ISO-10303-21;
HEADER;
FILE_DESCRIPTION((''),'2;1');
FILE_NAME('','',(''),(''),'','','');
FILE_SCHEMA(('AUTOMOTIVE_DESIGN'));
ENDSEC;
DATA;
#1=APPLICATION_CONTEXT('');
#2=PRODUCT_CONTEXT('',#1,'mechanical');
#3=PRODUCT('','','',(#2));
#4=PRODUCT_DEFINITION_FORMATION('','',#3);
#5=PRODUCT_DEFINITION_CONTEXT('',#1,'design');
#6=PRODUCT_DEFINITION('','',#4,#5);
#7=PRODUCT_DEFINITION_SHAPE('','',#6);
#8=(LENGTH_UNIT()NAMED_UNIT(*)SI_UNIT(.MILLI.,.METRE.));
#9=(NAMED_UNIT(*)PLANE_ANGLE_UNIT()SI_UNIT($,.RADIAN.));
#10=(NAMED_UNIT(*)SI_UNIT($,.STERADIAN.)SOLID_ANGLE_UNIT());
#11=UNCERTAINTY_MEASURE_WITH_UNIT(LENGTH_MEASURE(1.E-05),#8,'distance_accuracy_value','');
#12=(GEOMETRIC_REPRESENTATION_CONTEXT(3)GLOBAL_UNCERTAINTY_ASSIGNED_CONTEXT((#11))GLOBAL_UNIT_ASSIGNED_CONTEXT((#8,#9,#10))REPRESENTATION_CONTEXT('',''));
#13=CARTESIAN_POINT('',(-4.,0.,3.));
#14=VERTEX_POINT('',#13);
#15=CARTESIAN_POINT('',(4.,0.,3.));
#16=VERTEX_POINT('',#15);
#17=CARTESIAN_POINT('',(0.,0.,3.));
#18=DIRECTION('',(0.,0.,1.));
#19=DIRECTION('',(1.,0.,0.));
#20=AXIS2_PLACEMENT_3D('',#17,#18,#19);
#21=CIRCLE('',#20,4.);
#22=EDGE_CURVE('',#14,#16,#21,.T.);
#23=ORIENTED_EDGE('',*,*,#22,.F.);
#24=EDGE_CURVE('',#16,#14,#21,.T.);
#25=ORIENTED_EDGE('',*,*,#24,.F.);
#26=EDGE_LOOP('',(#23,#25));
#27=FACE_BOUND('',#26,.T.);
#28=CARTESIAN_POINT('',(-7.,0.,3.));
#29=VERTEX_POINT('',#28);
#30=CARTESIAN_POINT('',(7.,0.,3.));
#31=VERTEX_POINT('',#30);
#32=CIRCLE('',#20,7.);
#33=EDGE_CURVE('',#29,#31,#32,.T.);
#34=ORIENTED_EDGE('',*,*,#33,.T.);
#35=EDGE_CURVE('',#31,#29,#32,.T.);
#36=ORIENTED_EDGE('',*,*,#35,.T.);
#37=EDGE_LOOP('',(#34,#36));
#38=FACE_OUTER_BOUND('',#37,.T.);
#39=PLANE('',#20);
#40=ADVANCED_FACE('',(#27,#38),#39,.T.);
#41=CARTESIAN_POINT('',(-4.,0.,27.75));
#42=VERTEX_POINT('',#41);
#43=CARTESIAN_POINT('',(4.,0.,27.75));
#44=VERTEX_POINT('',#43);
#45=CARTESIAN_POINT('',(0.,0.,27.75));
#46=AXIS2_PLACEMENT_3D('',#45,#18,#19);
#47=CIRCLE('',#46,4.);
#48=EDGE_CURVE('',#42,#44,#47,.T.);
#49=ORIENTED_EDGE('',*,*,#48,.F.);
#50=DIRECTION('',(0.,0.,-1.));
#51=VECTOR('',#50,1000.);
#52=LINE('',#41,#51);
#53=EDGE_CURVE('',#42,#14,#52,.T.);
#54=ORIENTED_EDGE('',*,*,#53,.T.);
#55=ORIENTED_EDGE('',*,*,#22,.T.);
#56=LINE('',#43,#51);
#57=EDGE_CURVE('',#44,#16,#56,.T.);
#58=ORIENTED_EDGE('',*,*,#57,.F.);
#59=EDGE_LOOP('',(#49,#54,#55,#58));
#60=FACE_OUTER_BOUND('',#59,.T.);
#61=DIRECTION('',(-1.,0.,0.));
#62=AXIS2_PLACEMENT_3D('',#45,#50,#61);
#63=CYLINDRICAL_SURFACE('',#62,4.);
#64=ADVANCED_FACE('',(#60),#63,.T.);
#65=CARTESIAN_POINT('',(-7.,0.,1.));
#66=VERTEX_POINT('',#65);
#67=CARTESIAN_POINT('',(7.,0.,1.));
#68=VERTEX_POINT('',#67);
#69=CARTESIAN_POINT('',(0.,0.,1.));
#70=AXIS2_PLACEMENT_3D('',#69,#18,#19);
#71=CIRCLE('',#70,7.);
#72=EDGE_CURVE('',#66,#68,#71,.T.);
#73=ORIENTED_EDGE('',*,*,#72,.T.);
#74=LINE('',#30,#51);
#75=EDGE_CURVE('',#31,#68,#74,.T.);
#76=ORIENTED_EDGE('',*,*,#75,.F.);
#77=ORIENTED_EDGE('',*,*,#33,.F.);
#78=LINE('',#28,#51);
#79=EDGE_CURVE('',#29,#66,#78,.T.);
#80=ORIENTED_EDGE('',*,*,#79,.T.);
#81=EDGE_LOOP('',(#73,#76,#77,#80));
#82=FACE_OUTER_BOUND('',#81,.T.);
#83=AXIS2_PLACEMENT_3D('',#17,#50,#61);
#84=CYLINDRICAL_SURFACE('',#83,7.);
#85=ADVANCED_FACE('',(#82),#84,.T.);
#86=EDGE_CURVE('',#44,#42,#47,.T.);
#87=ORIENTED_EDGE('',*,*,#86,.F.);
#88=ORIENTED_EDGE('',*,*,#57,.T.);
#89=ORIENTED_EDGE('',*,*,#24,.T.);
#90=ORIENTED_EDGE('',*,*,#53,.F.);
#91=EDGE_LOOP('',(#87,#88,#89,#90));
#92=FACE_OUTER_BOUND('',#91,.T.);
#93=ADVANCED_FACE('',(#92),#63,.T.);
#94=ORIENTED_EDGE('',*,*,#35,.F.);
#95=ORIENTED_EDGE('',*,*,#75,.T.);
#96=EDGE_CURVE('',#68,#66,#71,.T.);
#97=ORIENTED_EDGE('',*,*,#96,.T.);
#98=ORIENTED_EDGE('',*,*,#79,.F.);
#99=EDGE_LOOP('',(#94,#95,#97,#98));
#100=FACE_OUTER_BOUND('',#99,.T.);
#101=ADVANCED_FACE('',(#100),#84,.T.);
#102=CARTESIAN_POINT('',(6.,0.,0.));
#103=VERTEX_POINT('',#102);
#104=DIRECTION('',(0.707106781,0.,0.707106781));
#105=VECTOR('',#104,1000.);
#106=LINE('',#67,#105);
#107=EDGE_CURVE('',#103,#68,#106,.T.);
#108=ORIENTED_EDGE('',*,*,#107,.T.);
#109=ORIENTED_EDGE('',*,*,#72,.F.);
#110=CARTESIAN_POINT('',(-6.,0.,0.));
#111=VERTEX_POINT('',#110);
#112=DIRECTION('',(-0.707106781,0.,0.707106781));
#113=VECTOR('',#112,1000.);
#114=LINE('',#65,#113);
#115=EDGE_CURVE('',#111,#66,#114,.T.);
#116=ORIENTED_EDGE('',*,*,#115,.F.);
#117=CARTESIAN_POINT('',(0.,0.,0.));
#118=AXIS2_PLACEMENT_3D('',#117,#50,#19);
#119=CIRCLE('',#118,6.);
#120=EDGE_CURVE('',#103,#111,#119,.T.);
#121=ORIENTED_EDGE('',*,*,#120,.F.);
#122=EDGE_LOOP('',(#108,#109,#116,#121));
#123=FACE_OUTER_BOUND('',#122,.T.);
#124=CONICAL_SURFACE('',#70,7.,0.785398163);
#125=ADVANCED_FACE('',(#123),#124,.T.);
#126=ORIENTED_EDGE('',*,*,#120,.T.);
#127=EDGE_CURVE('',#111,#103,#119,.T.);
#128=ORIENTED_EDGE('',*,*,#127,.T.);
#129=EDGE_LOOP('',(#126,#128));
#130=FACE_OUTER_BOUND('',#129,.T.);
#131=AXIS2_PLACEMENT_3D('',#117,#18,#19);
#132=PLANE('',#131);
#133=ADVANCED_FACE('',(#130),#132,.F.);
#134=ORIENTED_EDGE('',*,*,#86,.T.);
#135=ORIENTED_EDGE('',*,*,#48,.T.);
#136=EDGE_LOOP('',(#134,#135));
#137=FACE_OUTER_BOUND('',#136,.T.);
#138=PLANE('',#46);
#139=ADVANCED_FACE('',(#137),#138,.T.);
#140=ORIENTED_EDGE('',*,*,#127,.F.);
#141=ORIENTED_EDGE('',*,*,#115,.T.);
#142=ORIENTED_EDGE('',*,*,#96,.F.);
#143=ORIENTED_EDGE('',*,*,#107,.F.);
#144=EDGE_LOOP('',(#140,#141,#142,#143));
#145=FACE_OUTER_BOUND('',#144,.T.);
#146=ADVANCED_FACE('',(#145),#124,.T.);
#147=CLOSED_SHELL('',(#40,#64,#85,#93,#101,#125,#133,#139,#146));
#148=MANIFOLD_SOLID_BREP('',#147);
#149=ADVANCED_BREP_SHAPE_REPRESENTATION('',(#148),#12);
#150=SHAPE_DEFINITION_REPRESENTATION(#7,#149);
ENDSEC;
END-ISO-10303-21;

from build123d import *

# Parameters (mm, degrees)
HEAD_PROFILE_14_R      = 7
HEAD_14X3_DEPTH        = 3
SHANK_PROFILE_8_R      = 4
SHANK_8X24_75_DEPTH    = 24.75
HEAD_CHAMFER_1X45_SIZE = 1


with BuildPart() as part:
    # Head Profile Ø14 → Head Ø14x3 (new body)
    with BuildSketch(Plane.XY):
        Circle(HEAD_PROFILE_14_R)
    extrude(amount=HEAD_14X3_DEPTH)

    # Shank Profile Ø8 → Shank Ø8x24.75 (add)
    with BuildSketch(Plane.XY.offset(3)):
        Circle(SHANK_PROFILE_8_R)
    extrude(amount=SHANK_8X24_75_DEPTH)

    # Head Chamfer 1x45°
    head_chamfer_1x45_edges = [part.edges().sort_by_distance(p)[0] for p in [
        (-7, 0, 0),
    ]]
    chamfer(head_chamfer_1x45_edges, length=HEAD_CHAMFER_1X45_SIZE)


solid = part.part
